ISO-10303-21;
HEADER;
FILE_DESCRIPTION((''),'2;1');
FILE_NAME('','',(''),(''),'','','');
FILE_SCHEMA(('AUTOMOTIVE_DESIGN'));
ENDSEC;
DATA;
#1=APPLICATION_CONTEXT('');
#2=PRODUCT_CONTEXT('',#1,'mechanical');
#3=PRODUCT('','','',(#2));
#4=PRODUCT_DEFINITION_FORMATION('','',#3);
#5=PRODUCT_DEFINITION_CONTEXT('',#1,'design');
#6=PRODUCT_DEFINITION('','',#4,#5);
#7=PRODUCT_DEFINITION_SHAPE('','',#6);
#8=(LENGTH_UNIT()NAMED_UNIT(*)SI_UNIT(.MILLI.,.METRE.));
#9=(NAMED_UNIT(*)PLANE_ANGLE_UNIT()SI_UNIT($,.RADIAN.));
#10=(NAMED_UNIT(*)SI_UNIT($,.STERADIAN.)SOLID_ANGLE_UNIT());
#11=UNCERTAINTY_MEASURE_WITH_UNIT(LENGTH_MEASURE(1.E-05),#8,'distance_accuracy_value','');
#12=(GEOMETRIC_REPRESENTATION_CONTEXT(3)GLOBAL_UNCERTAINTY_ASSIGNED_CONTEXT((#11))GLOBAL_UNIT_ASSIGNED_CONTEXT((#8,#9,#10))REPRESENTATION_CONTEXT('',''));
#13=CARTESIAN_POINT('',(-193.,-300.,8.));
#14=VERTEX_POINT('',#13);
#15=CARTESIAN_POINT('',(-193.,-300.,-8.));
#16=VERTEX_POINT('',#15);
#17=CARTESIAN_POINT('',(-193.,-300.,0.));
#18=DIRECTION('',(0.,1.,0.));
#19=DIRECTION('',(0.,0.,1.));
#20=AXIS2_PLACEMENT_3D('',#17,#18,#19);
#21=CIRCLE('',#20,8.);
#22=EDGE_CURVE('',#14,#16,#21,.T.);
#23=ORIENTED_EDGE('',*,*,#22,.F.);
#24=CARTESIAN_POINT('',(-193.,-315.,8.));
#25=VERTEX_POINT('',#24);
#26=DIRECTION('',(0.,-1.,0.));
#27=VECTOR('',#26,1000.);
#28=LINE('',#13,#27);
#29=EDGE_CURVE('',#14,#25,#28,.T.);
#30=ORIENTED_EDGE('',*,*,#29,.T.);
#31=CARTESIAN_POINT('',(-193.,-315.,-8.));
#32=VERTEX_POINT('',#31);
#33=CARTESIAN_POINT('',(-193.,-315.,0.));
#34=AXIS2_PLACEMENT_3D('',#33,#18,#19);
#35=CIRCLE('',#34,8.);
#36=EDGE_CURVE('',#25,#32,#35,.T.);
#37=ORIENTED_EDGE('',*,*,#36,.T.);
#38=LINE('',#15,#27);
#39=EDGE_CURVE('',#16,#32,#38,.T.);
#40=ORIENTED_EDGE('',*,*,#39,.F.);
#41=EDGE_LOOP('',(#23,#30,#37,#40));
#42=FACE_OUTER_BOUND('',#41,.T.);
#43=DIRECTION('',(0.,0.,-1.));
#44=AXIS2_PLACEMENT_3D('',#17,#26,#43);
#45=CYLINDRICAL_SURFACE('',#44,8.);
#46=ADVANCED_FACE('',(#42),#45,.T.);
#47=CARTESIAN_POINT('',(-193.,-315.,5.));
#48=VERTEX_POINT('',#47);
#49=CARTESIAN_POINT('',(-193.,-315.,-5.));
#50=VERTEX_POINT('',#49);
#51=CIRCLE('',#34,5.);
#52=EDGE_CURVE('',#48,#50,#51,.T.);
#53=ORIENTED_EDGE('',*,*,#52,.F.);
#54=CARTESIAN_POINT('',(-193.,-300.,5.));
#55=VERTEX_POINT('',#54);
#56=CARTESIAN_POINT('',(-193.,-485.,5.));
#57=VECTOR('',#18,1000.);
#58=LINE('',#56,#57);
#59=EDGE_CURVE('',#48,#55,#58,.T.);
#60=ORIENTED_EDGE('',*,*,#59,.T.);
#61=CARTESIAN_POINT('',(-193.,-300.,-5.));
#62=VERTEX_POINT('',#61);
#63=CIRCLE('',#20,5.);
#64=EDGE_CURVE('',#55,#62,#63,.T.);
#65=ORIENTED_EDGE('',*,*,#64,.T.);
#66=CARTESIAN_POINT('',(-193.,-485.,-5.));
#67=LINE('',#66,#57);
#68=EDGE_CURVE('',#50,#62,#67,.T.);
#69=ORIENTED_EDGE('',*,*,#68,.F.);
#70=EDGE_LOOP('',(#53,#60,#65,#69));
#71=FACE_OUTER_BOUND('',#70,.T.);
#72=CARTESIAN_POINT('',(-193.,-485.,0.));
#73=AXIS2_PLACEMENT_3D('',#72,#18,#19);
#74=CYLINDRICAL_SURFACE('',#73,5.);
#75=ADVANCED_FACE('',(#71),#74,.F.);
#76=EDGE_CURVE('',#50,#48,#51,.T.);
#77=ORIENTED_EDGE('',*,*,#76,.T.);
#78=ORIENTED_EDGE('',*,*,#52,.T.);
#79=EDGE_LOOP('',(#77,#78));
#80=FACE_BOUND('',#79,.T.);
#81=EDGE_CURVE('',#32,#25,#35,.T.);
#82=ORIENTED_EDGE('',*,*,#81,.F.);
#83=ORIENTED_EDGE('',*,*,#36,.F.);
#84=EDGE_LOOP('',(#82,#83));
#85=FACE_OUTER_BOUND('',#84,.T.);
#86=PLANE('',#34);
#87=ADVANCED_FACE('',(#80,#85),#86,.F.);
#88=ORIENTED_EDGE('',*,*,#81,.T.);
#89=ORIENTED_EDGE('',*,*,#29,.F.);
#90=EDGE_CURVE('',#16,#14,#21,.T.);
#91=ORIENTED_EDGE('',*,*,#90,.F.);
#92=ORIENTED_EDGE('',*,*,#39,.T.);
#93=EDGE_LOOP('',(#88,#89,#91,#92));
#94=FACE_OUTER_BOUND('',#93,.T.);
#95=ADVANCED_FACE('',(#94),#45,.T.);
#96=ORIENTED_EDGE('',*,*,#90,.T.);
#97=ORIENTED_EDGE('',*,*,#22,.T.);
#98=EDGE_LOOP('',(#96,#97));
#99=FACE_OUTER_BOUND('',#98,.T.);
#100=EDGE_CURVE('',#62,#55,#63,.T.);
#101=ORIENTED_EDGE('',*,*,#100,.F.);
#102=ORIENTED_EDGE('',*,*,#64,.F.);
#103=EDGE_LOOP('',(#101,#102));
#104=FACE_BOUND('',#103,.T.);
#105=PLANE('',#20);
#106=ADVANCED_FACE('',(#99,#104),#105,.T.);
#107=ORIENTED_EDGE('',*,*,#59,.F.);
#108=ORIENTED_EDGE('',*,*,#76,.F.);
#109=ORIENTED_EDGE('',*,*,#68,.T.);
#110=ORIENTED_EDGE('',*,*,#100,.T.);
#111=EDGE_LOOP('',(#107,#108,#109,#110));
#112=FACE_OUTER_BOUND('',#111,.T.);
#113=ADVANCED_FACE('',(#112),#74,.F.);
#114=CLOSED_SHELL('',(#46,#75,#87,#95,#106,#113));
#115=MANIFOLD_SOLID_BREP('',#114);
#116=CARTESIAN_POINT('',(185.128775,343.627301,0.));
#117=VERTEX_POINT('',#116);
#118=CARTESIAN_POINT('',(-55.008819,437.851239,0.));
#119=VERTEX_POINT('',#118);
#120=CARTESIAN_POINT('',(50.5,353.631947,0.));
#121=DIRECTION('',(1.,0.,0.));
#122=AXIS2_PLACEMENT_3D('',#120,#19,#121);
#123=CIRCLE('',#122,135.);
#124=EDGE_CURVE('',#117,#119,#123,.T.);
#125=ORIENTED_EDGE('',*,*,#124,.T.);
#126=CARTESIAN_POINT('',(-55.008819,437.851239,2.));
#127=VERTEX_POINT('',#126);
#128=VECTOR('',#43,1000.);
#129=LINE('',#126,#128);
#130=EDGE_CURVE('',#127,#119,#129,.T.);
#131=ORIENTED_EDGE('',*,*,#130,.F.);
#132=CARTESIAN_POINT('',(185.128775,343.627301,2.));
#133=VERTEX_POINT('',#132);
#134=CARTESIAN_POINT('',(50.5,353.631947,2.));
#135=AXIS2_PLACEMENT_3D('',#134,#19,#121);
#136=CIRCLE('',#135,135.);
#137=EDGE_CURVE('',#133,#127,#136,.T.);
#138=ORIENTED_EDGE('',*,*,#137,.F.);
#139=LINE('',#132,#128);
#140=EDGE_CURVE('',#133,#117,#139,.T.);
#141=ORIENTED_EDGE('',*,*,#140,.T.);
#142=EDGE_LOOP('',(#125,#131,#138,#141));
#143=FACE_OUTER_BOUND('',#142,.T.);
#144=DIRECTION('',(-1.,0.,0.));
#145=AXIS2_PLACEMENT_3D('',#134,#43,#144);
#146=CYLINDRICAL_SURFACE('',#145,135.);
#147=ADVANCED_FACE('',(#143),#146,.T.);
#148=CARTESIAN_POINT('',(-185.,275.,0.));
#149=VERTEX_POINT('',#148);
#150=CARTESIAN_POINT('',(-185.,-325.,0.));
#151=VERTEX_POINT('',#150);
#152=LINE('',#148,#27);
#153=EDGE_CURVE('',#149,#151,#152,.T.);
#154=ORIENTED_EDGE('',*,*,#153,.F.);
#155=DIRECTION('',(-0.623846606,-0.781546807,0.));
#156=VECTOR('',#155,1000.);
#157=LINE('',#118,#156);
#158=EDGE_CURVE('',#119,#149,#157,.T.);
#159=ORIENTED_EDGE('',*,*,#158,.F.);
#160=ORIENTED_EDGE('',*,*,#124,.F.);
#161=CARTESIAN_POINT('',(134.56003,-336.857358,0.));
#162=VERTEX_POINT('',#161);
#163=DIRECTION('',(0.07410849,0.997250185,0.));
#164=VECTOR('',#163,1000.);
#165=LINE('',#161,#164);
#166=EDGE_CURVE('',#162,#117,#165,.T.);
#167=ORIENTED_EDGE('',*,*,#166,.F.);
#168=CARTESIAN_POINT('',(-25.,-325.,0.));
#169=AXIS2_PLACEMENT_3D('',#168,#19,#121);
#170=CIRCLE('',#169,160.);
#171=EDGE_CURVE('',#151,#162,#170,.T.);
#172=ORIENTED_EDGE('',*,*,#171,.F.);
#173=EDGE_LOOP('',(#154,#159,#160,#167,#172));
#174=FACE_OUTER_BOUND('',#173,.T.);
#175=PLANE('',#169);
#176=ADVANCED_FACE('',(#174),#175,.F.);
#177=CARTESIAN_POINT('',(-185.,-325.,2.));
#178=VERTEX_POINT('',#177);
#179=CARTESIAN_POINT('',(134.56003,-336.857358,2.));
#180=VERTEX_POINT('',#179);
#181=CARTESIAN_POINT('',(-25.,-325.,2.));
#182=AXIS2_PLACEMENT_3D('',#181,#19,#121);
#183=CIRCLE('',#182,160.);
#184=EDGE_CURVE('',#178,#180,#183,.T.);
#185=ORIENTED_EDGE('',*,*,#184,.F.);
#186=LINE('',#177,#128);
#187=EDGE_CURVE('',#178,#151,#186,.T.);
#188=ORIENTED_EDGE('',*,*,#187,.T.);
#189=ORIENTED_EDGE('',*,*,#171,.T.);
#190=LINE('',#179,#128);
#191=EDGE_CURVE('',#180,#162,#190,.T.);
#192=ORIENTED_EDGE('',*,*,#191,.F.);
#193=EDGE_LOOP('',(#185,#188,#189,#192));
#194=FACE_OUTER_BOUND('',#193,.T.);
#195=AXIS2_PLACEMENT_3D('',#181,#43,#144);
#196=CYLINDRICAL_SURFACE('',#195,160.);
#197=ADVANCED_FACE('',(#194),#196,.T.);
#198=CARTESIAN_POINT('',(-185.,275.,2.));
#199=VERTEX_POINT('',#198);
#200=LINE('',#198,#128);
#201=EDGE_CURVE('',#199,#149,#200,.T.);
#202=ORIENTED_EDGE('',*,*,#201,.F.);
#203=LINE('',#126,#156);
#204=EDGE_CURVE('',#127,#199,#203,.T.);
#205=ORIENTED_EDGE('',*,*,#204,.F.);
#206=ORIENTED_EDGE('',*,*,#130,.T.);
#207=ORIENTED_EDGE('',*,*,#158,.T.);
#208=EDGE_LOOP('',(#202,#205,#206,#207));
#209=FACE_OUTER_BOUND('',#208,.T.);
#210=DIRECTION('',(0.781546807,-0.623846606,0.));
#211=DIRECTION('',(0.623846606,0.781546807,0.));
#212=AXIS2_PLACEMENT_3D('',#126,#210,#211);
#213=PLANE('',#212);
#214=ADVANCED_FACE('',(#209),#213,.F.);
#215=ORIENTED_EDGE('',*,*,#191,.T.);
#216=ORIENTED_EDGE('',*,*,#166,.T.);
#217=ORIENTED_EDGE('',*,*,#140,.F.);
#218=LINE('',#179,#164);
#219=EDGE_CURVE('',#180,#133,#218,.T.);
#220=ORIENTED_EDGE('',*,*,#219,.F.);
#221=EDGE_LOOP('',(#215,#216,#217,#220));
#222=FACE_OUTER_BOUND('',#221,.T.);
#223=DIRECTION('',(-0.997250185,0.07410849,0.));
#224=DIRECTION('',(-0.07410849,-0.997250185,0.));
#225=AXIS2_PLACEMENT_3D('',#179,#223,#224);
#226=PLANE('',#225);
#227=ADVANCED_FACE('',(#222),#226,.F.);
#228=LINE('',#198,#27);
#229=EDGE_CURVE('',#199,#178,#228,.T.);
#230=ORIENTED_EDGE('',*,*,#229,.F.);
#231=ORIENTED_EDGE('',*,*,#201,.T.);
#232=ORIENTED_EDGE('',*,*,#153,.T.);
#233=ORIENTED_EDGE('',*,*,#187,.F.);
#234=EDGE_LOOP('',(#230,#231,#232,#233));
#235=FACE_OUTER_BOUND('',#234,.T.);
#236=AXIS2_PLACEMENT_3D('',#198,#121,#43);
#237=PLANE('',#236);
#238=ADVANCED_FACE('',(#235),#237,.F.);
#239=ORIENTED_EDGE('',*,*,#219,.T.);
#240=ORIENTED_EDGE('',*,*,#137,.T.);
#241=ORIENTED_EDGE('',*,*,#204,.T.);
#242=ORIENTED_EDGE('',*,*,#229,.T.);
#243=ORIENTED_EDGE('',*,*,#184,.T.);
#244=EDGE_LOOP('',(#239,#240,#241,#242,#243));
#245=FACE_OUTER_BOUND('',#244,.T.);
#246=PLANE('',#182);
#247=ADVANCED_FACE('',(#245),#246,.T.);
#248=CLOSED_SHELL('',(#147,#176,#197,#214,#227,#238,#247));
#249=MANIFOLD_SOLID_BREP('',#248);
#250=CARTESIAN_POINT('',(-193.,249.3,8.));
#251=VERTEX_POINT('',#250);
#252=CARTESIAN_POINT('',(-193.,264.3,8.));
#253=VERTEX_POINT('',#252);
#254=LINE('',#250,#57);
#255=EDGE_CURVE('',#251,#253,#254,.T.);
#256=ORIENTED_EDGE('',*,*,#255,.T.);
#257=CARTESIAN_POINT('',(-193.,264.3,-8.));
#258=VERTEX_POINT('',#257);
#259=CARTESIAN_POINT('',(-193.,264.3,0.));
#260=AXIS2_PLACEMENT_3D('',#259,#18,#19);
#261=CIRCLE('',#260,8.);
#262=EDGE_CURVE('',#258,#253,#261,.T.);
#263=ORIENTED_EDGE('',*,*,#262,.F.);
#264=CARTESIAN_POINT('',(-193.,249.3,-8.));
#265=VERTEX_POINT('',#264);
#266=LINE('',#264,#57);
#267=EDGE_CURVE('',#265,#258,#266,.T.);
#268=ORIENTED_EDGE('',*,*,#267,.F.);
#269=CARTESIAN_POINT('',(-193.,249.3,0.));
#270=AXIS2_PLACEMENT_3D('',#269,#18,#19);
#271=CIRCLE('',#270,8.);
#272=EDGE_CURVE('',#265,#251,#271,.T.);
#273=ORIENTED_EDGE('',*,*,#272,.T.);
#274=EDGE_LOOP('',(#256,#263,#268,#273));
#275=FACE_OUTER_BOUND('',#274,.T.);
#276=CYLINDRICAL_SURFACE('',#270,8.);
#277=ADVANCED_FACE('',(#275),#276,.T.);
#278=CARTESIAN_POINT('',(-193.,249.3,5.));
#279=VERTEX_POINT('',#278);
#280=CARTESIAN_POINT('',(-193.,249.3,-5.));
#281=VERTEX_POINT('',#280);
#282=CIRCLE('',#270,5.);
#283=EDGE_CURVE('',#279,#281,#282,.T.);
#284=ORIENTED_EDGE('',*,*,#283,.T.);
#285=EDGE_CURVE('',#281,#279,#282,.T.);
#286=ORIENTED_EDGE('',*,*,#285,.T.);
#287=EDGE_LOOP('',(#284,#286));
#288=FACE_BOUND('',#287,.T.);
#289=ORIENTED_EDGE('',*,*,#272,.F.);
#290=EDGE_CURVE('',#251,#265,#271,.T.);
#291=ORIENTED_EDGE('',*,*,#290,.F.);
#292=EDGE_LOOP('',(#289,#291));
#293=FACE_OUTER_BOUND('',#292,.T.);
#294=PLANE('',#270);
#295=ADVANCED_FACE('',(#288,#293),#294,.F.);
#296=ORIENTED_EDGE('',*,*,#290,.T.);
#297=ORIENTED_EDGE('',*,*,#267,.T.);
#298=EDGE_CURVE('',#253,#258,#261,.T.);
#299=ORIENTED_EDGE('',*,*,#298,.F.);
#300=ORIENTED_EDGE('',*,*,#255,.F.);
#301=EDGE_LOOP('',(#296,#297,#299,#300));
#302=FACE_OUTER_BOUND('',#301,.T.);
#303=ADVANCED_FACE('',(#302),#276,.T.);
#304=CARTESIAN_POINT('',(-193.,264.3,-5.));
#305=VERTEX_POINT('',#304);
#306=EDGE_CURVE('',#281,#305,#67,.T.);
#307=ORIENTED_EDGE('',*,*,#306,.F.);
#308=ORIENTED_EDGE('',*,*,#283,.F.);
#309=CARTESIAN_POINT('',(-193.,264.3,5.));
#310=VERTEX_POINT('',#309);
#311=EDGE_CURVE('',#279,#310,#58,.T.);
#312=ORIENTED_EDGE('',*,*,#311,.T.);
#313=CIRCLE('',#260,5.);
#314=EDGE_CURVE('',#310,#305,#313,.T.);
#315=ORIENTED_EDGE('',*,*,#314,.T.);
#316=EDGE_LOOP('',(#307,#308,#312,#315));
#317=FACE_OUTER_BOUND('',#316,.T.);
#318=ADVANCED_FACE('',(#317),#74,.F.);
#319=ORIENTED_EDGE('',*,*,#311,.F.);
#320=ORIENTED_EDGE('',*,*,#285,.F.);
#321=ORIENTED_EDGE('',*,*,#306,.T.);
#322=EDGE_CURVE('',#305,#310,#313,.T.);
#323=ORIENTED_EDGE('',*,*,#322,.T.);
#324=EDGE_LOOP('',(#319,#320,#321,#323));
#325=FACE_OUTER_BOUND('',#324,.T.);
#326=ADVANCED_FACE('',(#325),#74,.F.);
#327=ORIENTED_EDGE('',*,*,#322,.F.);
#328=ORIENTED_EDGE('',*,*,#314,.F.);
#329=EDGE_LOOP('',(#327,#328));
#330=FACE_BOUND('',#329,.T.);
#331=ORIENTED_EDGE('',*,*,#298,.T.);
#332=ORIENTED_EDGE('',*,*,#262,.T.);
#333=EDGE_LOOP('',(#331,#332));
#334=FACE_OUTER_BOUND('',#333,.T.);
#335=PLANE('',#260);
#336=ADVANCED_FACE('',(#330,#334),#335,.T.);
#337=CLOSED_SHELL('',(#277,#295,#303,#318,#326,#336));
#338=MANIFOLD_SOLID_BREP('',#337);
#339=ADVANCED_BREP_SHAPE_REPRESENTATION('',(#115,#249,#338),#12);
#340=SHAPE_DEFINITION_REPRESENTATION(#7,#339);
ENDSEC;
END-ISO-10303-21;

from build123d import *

# Parameters (mm, degrees)
EXTRUDE_1_DEPTH          = 2
SKETCH_2_R               = 8
EXTRUDE_2_DEPTH          = 15
SKETCH_3_R               = 8
EXTRUDE_3_DEPTH          = 15
CUT_EXTRUDE_1_DEPTH      = 776.832127461
CUT_EXTRUDE_1_DEPTH_BACK = 776.832127461
SKETCH_5_R               = 5


with BuildPart() as part:
    # 草图1 → 凸台-拉伸1 (new body)
    with BuildSketch(Plane.XY):
        with BuildLine():
            Line((134.560029616, -336.857358431), (185.128774988, 343.627300614))
            ThreePointArc((185.128774988, 343.627300614), (99.810552442, 479.304017745), (-55.008818994, 437.85123861))
            Line((-55.008818994, 437.85123861), (-185, 275))
            Line((-185, 275), (-185, -325))
            ThreePointArc((-185, -325), (-30.932759116, -484.889969571), (134.560029616, -336.857358431))
        make_face()
    extrude(amount=EXTRUDE_1_DEPTH)


with BuildPart() as body_2:
    # 草图2 → 凸台-拉伸2 (new body)
    with BuildSketch(Plane(origin=(0, -315, 0), x_dir=(1, 0, 0), z_dir=(0, 1, 0))):
        with Locations(Location((-193, 0, 0), (0, 0, 270))):
            Circle(SKETCH_2_R)
    extrude(amount=EXTRUDE_2_DEPTH)


with BuildPart() as body_3:
    # 草图3 → 凸台-拉伸3 (new body)
    with BuildSketch(Plane(origin=(0, 264.3, 0), x_dir=(1, 0, 0), z_dir=(0, 1, 0))):
        with Locations(Location((-193, 0, 0), (0, 0, 270))):
            Circle(SKETCH_3_R)
    extrude(amount=-EXTRUDE_3_DEPTH)


with BuildPart() as cut_extrude_1_tool:
    # 草图5 → 切除-拉伸1 (new, two sides: drawn at the far end of the back side and taken through both)
    with BuildSketch(Plane(origin=(0, 264.3, 0), x_dir=(1, 0, 0), z_dir=(0, 1, 0)).offset(-CUT_EXTRUDE_1_DEPTH_BACK)):
        with Locations(Location((-193, 0, 0), (0, 0, 270))):
            Circle(SKETCH_5_R)
    extrude(amount=CUT_EXTRUDE_1_DEPTH + CUT_EXTRUDE_1_DEPTH_BACK)


with BuildPart() as body_2_1:
    add(body_2.part)

    # 切除-拉伸1: cut by cut_extrude_1_tool
    add(cut_extrude_1_tool.part, mode=Mode.SUBTRACT)


with BuildPart() as body_3_1:
    add(body_3.part)

    # 切除-拉伸1: cut by cut_extrude_1_tool
    add(cut_extrude_1_tool.part, mode=Mode.SUBTRACT)


solid = Compound([part.part, body_2_1.part, body_3_1.part])
